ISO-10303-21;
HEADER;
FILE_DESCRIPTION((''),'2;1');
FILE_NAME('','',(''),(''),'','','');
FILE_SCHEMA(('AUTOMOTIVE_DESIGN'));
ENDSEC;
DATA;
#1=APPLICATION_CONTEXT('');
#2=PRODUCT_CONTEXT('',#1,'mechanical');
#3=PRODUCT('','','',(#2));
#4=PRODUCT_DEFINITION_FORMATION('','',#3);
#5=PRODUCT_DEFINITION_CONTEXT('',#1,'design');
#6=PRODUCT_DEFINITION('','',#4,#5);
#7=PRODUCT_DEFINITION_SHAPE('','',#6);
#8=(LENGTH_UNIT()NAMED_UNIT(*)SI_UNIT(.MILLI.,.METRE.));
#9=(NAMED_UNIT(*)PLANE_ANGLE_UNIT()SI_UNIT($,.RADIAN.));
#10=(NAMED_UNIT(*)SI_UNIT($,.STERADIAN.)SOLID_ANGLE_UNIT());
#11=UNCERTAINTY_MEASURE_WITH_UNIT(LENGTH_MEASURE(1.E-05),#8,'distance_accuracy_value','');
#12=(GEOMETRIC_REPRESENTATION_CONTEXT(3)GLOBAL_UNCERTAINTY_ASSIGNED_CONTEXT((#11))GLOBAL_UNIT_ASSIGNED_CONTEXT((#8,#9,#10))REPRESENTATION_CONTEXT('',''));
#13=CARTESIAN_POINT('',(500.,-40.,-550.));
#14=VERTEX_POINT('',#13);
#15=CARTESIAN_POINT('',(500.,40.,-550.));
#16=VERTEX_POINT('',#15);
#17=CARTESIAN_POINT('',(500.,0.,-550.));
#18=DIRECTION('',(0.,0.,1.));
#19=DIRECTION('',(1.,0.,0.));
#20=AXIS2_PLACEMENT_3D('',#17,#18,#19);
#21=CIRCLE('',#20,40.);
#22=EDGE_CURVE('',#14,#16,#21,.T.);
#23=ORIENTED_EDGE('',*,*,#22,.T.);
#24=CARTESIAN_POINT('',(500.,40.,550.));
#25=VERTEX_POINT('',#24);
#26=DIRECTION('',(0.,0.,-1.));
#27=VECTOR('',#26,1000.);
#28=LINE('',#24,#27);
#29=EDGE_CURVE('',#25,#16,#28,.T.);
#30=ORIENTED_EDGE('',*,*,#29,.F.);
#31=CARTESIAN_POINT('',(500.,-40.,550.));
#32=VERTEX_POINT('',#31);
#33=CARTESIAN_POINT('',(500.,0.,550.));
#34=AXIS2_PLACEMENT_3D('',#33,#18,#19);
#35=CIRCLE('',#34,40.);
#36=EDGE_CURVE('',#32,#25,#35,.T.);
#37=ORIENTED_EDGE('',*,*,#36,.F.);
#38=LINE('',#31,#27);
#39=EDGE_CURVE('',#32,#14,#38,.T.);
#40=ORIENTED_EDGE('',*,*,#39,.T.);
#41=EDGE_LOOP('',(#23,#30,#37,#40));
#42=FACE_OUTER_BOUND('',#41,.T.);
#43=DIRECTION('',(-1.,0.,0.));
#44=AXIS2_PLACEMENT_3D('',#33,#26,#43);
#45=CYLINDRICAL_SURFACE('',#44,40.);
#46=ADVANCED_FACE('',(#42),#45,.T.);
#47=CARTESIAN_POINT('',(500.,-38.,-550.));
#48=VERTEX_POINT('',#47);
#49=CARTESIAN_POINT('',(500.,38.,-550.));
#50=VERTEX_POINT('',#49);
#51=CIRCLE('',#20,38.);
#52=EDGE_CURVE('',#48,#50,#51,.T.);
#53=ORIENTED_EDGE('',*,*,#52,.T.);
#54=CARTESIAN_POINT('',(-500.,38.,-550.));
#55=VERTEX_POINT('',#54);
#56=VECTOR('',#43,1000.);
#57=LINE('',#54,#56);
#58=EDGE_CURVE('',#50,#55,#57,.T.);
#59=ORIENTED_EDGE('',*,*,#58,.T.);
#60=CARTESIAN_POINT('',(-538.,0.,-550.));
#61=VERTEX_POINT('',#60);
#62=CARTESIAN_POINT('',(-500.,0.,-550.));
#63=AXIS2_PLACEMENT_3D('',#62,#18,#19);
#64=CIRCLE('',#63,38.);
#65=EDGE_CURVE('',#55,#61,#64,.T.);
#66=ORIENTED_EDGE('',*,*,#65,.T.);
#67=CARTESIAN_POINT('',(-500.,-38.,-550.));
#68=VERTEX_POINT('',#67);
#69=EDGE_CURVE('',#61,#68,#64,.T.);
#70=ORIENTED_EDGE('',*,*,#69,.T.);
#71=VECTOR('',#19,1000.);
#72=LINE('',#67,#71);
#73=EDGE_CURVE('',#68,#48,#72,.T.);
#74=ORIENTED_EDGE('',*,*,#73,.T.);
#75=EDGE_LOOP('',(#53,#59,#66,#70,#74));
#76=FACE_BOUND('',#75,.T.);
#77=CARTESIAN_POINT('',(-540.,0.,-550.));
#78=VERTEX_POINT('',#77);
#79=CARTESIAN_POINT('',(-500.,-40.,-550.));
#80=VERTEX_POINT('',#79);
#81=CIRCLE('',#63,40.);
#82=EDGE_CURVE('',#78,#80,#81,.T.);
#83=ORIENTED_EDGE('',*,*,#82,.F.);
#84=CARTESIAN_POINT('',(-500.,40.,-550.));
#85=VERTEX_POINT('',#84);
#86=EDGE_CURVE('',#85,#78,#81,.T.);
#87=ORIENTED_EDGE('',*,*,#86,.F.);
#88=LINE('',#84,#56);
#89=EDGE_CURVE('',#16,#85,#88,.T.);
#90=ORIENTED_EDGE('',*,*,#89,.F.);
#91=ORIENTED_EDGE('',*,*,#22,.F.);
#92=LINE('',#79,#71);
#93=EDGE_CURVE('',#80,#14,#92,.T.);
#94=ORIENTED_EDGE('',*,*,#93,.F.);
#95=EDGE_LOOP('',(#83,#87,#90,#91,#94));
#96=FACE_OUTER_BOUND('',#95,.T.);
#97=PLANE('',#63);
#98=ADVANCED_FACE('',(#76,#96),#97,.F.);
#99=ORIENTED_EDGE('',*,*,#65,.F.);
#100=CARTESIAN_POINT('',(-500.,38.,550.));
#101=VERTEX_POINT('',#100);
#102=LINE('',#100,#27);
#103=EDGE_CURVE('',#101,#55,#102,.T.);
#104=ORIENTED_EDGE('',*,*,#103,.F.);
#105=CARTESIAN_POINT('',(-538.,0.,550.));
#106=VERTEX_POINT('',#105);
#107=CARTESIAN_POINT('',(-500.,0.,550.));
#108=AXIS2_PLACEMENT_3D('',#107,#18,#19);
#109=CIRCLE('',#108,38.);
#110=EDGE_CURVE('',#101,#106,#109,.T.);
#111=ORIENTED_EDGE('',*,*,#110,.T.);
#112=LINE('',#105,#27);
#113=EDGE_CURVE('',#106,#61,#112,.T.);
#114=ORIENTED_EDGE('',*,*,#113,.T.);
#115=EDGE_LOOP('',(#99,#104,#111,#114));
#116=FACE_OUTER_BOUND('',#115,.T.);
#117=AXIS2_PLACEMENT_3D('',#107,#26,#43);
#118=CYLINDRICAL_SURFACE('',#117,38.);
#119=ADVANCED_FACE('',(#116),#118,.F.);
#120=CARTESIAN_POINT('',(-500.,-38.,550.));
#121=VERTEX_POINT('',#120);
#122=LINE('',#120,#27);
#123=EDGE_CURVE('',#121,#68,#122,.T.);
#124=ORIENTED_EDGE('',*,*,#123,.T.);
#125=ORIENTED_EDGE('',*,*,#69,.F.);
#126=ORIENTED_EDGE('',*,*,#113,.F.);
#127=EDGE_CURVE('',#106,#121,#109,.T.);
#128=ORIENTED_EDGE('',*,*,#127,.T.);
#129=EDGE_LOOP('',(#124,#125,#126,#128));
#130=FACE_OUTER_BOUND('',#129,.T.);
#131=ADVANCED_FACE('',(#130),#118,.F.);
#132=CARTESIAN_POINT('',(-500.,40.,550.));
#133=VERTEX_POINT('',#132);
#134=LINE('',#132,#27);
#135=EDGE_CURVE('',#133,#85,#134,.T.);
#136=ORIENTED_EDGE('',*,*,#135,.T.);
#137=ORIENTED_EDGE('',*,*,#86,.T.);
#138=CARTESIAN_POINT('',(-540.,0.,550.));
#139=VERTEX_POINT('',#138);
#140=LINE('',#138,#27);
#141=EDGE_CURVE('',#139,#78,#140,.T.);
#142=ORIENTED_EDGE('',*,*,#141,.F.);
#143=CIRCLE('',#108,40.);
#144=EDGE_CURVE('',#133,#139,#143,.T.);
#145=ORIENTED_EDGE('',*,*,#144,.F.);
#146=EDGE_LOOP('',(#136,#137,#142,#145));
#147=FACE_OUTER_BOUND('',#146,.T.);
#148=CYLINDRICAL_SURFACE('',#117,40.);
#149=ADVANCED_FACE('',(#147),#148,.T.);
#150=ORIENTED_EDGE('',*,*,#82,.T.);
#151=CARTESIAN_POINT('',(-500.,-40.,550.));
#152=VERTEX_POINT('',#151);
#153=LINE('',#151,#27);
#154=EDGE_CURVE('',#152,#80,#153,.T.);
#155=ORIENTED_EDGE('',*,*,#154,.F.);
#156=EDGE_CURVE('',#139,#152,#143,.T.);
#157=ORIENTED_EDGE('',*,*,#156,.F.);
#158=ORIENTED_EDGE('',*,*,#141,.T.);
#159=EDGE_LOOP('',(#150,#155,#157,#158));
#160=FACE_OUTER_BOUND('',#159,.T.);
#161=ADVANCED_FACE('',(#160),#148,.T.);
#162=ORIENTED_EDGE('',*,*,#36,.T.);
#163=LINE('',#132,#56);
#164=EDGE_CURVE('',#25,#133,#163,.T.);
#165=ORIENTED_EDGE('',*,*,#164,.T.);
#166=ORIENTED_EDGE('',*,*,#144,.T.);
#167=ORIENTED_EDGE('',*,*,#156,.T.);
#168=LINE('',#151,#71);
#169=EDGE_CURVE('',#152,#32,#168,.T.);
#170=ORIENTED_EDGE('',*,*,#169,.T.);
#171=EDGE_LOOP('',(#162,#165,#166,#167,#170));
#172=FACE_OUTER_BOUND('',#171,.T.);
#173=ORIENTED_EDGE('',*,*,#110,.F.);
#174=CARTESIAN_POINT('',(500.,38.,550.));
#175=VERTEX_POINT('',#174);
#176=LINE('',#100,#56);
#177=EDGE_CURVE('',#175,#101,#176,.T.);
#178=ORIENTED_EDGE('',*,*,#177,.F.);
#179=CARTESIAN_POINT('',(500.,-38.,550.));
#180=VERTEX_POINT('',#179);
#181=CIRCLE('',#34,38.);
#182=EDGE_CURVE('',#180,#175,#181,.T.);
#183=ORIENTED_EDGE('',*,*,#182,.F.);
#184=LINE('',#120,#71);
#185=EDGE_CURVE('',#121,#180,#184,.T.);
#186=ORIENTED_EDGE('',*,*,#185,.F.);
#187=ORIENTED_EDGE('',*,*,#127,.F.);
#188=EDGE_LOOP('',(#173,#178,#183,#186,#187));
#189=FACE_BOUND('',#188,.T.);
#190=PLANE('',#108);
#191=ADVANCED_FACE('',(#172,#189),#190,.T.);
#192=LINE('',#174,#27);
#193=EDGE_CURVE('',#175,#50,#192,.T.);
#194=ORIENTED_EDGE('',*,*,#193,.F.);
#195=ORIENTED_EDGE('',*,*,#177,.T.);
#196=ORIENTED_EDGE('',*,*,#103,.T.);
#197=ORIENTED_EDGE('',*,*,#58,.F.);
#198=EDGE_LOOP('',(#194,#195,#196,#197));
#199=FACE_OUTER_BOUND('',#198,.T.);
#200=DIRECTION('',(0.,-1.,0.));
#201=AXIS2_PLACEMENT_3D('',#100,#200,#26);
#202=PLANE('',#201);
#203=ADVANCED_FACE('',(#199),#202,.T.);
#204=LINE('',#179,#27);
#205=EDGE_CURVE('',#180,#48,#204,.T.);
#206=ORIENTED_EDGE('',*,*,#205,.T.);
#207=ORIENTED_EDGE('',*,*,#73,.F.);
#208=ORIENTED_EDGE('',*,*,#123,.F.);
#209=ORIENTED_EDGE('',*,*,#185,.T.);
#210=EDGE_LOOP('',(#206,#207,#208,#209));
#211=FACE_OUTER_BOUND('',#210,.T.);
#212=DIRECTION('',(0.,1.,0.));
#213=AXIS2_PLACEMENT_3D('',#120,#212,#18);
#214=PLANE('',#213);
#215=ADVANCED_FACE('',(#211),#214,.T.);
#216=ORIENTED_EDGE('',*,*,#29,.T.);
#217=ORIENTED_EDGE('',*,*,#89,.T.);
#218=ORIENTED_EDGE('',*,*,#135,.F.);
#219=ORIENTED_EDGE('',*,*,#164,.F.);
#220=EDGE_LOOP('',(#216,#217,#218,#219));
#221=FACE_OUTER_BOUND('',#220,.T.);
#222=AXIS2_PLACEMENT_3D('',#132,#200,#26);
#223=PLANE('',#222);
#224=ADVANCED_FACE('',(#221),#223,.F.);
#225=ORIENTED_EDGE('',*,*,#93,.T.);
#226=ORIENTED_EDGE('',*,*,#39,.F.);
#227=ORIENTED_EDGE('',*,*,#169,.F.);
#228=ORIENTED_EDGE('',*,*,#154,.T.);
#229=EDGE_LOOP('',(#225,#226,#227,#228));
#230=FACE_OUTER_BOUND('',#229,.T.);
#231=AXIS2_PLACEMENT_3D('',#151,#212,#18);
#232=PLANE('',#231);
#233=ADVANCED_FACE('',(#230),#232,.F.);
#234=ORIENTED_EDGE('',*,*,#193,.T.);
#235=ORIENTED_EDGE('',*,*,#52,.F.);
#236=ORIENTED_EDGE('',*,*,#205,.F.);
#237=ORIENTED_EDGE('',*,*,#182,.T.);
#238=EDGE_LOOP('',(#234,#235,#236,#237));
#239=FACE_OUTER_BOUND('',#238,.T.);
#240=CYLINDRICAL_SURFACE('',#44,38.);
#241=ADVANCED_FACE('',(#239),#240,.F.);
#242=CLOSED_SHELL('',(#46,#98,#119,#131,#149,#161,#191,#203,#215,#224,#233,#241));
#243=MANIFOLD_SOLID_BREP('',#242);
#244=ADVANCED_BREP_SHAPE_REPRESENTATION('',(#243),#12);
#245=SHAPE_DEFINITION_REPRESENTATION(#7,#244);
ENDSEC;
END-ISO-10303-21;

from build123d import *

# Parameters (mm, degrees)
EXTRUDE_1_DEPTH = 550


with BuildPart() as part:
    # 草图1 → 拉伸-薄壁1 (new, symmetric)
    with BuildSketch(Plane.XY):
        with BuildLine():
            Line((500, -40), (-500, -40))
            ThreePointArc((-500, -40), (-540, 0), (-500, 40))
            Line((-500, 40), (500, 40))
            ThreePointArc((500, 40), (540, 0), (500, -40))
        make_face()
        with BuildLine():
            Line((500, -38), (-500, -38))
            ThreePointArc((-500, -38), (-538, 0), (-500, 38))
            Line((-500, 38), (500, 38))
            ThreePointArc((500, 38), (538, 0), (500, -38))
        make_face(mode=Mode.SUBTRACT)
    extrude(amount=EXTRUDE_1_DEPTH, both=True)


solid = part.part
